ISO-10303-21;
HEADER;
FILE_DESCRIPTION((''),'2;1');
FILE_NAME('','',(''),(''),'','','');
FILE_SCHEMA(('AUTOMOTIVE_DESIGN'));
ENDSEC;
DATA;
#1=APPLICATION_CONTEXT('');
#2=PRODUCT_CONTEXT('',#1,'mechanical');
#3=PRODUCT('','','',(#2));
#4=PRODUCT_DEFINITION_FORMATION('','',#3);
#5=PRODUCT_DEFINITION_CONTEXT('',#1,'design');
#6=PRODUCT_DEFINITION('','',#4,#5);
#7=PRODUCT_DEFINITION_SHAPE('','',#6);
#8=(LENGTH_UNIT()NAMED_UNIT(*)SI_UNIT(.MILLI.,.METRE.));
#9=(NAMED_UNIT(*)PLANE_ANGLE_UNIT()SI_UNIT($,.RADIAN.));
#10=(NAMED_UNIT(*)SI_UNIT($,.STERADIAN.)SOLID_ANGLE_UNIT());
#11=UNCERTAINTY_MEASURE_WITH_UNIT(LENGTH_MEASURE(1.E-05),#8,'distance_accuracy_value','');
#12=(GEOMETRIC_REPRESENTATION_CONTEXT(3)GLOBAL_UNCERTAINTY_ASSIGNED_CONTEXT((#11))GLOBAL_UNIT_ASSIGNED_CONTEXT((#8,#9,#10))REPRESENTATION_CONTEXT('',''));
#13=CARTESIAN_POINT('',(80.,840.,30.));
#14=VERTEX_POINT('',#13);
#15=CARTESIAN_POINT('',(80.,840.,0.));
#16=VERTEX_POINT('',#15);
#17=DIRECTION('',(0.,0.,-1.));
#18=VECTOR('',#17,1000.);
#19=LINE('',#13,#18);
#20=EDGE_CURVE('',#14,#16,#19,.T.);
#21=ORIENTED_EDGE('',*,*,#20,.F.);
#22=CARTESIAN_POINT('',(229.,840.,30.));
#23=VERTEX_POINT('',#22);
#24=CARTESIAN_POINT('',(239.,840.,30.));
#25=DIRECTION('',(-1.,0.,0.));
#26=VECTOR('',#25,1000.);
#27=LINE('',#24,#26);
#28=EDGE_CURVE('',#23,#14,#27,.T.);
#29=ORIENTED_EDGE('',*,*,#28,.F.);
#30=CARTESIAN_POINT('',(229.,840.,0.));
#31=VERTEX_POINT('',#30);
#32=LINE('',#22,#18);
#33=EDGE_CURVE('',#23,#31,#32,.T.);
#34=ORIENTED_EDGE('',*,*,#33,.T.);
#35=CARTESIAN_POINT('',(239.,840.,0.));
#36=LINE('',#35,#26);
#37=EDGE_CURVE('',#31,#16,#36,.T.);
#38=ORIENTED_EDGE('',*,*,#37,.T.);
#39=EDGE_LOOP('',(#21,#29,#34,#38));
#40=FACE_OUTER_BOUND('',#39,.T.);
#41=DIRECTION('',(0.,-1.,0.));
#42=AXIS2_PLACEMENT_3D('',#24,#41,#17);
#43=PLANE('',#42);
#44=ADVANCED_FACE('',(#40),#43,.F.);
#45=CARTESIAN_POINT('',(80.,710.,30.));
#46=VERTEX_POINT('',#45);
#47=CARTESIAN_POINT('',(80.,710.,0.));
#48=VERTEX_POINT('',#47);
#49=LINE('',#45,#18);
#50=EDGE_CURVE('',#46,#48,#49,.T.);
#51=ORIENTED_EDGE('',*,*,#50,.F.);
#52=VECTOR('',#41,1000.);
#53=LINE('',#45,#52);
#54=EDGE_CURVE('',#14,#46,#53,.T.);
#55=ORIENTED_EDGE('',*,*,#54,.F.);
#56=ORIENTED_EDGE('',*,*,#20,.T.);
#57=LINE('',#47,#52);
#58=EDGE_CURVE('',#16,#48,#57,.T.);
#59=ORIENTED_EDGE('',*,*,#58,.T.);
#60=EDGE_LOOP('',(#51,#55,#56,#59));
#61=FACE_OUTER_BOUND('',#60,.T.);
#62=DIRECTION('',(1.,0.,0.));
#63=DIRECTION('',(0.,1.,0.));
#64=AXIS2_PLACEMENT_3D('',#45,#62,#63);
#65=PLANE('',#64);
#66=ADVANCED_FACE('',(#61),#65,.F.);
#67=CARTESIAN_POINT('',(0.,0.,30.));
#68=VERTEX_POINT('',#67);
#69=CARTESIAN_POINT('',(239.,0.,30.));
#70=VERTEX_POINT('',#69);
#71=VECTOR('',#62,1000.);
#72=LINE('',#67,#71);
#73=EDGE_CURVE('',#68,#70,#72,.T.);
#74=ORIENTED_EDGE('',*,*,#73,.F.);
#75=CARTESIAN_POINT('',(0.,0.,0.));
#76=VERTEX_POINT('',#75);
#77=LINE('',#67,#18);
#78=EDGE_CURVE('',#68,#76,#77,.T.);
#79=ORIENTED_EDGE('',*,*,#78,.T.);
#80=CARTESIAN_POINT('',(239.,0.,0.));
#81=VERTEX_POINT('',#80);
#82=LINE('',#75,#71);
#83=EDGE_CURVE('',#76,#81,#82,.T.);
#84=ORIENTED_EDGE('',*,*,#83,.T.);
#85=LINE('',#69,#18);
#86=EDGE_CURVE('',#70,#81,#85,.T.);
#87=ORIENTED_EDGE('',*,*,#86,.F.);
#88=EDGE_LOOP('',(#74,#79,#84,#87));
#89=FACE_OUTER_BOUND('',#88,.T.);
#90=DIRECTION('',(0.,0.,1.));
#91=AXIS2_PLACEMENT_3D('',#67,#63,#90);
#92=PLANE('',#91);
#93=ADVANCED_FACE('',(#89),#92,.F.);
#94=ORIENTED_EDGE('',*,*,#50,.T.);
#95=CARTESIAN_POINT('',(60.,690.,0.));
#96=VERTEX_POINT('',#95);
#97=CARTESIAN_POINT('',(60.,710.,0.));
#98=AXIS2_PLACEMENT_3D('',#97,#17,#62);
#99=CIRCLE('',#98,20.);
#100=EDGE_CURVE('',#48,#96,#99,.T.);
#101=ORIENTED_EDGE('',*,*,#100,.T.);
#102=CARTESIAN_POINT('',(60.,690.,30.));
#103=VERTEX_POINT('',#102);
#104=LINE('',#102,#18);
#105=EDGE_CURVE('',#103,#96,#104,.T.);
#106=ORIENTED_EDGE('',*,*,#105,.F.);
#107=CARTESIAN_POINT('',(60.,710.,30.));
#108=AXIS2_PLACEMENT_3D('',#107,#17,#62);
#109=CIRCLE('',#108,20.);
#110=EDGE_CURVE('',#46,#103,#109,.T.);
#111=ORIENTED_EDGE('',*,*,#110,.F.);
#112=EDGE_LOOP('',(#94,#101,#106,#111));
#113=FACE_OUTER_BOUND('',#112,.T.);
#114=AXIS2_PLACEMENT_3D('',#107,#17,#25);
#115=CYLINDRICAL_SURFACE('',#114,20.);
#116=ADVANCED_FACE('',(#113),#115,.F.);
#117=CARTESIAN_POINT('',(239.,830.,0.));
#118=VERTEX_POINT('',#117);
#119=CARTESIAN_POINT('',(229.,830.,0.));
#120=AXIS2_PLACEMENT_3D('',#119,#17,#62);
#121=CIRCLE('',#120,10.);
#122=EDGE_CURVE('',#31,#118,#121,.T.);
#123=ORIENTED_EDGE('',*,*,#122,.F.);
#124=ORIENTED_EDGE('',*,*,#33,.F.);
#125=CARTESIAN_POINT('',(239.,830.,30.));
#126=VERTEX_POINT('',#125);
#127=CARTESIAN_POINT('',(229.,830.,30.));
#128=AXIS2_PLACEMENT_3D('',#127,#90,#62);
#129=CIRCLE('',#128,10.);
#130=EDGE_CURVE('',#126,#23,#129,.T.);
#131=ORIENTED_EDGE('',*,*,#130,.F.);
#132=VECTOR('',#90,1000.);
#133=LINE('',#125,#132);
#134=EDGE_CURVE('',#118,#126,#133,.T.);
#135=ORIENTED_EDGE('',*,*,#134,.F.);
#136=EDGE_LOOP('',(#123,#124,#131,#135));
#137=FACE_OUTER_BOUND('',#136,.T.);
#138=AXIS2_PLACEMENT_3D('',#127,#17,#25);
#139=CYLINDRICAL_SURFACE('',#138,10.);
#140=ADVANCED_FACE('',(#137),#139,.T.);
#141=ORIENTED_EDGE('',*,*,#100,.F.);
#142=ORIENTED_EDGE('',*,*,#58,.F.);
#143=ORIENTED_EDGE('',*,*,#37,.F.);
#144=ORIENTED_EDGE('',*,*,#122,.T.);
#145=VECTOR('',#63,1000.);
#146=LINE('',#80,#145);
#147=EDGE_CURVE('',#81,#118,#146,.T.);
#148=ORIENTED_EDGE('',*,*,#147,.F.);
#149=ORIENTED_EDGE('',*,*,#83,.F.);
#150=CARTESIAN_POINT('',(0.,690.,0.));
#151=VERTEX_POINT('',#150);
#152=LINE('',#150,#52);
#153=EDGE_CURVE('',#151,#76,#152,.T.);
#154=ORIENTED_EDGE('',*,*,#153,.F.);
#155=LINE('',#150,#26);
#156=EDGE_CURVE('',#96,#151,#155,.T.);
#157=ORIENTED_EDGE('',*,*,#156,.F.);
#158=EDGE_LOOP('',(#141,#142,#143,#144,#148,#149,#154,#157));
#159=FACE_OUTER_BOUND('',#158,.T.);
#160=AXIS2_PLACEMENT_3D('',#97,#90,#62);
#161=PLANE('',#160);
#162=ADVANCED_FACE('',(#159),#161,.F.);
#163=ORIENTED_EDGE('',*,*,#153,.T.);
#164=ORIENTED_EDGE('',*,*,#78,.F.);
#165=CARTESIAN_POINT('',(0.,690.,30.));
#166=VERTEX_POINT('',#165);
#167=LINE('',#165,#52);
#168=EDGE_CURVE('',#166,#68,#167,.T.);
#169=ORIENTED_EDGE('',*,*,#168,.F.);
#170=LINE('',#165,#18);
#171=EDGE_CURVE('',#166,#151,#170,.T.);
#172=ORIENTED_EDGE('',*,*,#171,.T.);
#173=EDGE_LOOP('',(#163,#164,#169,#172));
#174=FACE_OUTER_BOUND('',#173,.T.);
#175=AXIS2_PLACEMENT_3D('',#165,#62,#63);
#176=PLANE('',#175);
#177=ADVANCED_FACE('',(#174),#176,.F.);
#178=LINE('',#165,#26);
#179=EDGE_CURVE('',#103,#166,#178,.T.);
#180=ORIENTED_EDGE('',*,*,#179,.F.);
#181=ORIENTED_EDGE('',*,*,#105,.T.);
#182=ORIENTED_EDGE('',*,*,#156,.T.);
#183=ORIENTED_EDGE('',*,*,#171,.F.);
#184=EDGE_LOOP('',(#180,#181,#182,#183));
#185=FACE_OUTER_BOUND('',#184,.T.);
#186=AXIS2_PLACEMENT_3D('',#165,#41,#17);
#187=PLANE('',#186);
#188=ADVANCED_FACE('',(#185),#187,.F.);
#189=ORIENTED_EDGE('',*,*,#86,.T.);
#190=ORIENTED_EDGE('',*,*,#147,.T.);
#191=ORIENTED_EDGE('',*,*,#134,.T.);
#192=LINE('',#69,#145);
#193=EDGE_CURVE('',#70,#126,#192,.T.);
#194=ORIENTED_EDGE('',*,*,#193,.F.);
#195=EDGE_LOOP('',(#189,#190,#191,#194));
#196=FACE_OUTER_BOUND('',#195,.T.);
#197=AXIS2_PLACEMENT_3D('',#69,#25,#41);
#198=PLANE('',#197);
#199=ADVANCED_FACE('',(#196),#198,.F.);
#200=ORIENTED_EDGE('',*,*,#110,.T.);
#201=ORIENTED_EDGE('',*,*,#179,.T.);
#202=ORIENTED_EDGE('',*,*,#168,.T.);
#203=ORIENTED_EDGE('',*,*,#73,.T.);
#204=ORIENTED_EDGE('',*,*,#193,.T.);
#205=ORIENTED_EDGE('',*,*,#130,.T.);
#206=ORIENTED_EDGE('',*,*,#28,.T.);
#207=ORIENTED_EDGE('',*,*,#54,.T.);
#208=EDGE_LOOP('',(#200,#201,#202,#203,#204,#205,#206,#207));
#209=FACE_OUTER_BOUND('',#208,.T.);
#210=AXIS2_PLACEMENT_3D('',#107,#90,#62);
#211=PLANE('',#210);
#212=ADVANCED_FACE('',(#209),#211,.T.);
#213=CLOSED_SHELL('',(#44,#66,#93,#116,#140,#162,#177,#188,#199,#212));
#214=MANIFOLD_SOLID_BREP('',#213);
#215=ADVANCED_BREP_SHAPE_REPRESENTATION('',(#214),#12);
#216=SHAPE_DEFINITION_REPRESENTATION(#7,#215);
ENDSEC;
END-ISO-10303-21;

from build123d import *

# Parameters (mm, degrees)
BOSS_EXTRUDE1_DEPTH = 30
FILLET1_R           = 10


with BuildPart() as part:
    # Sketch1 → Boss-Extrude1 (new body)
    with BuildSketch(Plane.XY):
        with BuildLine():
            Line((0, 0), (239, 0))
            Line((239, 0), (239, 840))
            Line((239, 840), (80, 840))
            Line((80, 840), (80, 710))
            ThreePointArc((80, 710), (74.142135624, 695.857864376), (60, 690))
            Line((60, 690), (0, 690))
            Line((0, 690), (0, 0))
        make_face()
    extrude(amount=BOSS_EXTRUDE1_DEPTH)

    # Fillet1
    fillet1_edges = [part.edges().sort_by_distance(p)[0] for p in [
        (239, 840, 15),
    ]]
    fillet(fillet1_edges, radius=FILLET1_R)


solid = part.part
